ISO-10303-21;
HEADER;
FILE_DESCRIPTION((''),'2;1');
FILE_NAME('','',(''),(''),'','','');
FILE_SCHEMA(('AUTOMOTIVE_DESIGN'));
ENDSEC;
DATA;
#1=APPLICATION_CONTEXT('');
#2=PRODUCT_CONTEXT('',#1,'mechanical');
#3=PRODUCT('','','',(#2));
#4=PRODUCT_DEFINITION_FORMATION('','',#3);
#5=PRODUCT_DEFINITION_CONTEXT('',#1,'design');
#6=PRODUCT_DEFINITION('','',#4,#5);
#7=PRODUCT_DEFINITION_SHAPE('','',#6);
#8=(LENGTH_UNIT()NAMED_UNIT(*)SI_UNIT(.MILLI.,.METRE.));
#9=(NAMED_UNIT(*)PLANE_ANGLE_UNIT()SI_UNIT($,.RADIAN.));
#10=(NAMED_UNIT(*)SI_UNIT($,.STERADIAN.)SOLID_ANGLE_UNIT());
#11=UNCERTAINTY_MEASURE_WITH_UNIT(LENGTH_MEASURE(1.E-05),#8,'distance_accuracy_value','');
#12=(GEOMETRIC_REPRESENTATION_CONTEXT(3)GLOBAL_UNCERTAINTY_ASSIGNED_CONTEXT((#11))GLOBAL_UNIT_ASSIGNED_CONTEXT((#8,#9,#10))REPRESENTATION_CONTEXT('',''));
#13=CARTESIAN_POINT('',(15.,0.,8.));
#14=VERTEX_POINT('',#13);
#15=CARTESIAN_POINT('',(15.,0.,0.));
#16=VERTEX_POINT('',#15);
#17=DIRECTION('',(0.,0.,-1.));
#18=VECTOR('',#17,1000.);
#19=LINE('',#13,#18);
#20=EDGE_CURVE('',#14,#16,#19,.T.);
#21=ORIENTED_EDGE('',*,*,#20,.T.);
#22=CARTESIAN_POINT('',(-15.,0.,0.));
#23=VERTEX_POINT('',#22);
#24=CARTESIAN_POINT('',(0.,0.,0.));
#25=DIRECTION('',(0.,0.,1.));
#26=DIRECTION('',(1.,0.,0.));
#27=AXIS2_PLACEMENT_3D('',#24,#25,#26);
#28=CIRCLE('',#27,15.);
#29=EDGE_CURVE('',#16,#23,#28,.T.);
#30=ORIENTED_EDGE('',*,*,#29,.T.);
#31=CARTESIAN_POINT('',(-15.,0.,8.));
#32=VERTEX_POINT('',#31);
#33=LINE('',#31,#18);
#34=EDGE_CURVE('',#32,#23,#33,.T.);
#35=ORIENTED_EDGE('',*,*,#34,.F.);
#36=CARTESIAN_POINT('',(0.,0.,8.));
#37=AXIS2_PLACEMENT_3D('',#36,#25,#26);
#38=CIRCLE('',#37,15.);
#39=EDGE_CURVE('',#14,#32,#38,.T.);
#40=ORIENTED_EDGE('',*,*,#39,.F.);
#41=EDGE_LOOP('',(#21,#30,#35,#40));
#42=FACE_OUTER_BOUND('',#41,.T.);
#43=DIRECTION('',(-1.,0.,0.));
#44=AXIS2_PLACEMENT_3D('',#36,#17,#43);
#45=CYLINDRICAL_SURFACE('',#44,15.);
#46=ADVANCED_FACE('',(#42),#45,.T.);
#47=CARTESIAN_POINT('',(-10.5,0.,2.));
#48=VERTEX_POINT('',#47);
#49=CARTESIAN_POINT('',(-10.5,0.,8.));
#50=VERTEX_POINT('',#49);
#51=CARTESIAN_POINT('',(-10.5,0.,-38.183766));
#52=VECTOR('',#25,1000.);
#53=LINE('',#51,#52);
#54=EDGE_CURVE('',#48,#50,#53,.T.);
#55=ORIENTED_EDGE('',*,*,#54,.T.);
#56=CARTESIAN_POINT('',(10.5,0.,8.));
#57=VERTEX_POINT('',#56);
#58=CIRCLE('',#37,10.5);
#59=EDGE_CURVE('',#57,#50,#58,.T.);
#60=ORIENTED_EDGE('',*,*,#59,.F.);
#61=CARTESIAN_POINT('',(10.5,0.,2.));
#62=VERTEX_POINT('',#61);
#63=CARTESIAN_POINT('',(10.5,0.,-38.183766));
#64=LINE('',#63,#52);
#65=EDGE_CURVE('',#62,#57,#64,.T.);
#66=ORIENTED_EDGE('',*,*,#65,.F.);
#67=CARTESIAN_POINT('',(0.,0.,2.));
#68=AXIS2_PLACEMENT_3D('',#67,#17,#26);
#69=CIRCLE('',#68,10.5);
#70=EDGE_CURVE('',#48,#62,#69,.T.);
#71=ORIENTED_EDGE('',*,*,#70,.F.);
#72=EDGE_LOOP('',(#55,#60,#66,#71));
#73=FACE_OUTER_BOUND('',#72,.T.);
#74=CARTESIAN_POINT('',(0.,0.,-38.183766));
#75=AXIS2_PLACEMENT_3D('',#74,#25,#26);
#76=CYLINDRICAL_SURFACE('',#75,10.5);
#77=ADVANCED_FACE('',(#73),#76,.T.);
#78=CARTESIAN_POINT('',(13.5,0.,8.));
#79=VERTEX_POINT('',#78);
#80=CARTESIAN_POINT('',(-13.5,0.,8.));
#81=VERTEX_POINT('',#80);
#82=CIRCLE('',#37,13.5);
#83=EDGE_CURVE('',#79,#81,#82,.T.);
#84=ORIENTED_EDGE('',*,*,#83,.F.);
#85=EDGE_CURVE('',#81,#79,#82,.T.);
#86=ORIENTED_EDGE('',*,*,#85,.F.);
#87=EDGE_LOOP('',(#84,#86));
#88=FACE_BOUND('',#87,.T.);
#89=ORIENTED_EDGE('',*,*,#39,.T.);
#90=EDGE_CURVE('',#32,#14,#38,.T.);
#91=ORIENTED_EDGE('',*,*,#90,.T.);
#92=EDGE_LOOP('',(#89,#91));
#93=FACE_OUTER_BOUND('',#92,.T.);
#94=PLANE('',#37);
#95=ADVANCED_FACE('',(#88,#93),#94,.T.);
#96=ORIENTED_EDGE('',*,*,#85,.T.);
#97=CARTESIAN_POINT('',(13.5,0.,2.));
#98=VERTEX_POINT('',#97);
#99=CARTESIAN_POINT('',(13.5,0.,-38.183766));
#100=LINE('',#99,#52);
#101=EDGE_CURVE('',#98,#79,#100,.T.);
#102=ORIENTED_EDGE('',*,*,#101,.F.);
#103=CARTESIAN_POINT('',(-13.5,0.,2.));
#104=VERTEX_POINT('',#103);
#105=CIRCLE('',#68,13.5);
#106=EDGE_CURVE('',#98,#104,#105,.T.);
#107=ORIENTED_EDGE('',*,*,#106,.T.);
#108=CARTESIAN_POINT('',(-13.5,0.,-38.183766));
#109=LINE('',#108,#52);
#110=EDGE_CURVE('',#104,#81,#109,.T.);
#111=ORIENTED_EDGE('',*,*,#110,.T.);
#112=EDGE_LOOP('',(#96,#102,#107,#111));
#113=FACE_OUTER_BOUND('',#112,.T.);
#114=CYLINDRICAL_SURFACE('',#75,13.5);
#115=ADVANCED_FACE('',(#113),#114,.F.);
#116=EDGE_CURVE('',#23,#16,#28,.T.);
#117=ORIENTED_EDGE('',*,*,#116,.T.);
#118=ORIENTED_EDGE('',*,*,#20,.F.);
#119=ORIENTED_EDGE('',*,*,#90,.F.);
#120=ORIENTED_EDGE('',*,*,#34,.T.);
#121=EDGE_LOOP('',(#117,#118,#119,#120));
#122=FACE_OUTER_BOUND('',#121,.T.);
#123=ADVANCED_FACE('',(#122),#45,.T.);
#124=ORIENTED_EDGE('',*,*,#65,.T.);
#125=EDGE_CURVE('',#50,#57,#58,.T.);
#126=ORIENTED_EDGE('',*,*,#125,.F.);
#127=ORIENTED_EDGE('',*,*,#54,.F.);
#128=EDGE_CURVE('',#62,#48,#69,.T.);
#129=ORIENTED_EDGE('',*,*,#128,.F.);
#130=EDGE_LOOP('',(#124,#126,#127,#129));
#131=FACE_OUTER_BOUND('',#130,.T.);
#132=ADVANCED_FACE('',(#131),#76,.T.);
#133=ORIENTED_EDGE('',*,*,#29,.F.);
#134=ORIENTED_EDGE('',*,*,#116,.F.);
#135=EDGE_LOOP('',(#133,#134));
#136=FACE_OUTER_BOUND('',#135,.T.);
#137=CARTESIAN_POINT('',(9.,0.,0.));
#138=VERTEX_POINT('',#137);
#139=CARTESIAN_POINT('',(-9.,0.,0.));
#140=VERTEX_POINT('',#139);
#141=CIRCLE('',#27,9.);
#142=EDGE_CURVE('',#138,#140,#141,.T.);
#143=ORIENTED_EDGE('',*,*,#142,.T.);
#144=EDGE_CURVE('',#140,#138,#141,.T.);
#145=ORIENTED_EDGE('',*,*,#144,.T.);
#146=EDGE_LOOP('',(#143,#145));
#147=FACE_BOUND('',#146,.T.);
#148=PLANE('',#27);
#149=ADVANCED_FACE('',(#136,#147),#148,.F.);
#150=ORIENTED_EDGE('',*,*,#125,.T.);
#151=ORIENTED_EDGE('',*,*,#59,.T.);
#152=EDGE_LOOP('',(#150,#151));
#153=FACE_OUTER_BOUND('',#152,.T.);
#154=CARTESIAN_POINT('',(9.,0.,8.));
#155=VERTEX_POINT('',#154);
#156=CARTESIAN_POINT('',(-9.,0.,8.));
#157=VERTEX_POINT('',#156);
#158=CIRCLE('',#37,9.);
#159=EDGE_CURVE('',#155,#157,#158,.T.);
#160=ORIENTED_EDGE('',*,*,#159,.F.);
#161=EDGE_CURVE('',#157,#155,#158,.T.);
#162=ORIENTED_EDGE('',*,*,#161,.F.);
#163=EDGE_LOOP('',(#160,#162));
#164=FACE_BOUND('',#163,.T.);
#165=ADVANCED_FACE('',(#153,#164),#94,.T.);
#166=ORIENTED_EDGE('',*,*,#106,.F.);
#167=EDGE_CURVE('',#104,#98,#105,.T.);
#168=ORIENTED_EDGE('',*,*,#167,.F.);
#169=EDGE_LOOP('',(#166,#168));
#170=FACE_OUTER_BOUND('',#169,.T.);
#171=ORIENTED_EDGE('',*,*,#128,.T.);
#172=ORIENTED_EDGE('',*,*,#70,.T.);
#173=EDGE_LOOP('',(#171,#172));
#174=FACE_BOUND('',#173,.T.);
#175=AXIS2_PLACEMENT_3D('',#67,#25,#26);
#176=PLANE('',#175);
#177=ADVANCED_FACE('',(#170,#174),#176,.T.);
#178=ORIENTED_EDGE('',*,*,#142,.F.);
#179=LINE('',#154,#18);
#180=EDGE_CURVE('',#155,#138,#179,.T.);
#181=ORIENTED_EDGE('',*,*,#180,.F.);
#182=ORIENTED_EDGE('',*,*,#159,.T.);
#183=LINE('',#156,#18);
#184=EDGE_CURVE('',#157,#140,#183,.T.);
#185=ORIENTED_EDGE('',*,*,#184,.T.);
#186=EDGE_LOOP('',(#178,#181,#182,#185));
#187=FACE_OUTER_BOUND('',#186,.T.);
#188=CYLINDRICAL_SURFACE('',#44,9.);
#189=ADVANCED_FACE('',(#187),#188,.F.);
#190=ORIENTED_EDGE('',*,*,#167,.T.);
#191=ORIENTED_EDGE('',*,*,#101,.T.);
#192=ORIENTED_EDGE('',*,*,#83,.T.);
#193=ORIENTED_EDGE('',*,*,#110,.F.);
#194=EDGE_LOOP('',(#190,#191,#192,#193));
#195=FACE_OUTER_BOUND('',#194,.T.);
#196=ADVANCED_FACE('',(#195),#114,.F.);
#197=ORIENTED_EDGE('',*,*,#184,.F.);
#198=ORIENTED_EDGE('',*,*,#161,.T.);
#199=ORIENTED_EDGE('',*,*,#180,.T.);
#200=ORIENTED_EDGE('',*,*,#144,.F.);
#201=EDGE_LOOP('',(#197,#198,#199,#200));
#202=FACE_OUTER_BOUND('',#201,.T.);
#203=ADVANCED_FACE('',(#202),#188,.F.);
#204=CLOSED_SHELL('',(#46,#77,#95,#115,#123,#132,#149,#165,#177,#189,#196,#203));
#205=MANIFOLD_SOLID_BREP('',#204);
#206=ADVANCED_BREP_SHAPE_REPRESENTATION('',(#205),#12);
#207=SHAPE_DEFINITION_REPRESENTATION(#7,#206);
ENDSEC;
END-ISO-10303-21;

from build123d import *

# Parameters (mm, degrees)
SKETCH1_R           = 15
SKETCH1_R_2         = 9
BOSS_EXTRUDE1_DEPTH = 8
SKETCH2_R           = 13.5
SKETCH2_R_2         = 10.5
CUT_EXTRUDE1_DEPTH  = 6


with BuildPart() as part:
    # Sketch1 → Boss-Extrude1 (new body)
    with BuildSketch(Plane.XY):
        Circle(SKETCH1_R)
        Circle(SKETCH1_R_2, mode=Mode.SUBTRACT)
    extrude(amount=BOSS_EXTRUDE1_DEPTH)

    # Sketch2 → Cut-Extrude1 (cut)
    with BuildSketch(Plane.XY.offset(8)):
        Circle(SKETCH2_R)
        Circle(SKETCH2_R_2, mode=Mode.SUBTRACT)
    extrude(amount=-CUT_EXTRUDE1_DEPTH, mode=Mode.SUBTRACT)


solid = part.part
